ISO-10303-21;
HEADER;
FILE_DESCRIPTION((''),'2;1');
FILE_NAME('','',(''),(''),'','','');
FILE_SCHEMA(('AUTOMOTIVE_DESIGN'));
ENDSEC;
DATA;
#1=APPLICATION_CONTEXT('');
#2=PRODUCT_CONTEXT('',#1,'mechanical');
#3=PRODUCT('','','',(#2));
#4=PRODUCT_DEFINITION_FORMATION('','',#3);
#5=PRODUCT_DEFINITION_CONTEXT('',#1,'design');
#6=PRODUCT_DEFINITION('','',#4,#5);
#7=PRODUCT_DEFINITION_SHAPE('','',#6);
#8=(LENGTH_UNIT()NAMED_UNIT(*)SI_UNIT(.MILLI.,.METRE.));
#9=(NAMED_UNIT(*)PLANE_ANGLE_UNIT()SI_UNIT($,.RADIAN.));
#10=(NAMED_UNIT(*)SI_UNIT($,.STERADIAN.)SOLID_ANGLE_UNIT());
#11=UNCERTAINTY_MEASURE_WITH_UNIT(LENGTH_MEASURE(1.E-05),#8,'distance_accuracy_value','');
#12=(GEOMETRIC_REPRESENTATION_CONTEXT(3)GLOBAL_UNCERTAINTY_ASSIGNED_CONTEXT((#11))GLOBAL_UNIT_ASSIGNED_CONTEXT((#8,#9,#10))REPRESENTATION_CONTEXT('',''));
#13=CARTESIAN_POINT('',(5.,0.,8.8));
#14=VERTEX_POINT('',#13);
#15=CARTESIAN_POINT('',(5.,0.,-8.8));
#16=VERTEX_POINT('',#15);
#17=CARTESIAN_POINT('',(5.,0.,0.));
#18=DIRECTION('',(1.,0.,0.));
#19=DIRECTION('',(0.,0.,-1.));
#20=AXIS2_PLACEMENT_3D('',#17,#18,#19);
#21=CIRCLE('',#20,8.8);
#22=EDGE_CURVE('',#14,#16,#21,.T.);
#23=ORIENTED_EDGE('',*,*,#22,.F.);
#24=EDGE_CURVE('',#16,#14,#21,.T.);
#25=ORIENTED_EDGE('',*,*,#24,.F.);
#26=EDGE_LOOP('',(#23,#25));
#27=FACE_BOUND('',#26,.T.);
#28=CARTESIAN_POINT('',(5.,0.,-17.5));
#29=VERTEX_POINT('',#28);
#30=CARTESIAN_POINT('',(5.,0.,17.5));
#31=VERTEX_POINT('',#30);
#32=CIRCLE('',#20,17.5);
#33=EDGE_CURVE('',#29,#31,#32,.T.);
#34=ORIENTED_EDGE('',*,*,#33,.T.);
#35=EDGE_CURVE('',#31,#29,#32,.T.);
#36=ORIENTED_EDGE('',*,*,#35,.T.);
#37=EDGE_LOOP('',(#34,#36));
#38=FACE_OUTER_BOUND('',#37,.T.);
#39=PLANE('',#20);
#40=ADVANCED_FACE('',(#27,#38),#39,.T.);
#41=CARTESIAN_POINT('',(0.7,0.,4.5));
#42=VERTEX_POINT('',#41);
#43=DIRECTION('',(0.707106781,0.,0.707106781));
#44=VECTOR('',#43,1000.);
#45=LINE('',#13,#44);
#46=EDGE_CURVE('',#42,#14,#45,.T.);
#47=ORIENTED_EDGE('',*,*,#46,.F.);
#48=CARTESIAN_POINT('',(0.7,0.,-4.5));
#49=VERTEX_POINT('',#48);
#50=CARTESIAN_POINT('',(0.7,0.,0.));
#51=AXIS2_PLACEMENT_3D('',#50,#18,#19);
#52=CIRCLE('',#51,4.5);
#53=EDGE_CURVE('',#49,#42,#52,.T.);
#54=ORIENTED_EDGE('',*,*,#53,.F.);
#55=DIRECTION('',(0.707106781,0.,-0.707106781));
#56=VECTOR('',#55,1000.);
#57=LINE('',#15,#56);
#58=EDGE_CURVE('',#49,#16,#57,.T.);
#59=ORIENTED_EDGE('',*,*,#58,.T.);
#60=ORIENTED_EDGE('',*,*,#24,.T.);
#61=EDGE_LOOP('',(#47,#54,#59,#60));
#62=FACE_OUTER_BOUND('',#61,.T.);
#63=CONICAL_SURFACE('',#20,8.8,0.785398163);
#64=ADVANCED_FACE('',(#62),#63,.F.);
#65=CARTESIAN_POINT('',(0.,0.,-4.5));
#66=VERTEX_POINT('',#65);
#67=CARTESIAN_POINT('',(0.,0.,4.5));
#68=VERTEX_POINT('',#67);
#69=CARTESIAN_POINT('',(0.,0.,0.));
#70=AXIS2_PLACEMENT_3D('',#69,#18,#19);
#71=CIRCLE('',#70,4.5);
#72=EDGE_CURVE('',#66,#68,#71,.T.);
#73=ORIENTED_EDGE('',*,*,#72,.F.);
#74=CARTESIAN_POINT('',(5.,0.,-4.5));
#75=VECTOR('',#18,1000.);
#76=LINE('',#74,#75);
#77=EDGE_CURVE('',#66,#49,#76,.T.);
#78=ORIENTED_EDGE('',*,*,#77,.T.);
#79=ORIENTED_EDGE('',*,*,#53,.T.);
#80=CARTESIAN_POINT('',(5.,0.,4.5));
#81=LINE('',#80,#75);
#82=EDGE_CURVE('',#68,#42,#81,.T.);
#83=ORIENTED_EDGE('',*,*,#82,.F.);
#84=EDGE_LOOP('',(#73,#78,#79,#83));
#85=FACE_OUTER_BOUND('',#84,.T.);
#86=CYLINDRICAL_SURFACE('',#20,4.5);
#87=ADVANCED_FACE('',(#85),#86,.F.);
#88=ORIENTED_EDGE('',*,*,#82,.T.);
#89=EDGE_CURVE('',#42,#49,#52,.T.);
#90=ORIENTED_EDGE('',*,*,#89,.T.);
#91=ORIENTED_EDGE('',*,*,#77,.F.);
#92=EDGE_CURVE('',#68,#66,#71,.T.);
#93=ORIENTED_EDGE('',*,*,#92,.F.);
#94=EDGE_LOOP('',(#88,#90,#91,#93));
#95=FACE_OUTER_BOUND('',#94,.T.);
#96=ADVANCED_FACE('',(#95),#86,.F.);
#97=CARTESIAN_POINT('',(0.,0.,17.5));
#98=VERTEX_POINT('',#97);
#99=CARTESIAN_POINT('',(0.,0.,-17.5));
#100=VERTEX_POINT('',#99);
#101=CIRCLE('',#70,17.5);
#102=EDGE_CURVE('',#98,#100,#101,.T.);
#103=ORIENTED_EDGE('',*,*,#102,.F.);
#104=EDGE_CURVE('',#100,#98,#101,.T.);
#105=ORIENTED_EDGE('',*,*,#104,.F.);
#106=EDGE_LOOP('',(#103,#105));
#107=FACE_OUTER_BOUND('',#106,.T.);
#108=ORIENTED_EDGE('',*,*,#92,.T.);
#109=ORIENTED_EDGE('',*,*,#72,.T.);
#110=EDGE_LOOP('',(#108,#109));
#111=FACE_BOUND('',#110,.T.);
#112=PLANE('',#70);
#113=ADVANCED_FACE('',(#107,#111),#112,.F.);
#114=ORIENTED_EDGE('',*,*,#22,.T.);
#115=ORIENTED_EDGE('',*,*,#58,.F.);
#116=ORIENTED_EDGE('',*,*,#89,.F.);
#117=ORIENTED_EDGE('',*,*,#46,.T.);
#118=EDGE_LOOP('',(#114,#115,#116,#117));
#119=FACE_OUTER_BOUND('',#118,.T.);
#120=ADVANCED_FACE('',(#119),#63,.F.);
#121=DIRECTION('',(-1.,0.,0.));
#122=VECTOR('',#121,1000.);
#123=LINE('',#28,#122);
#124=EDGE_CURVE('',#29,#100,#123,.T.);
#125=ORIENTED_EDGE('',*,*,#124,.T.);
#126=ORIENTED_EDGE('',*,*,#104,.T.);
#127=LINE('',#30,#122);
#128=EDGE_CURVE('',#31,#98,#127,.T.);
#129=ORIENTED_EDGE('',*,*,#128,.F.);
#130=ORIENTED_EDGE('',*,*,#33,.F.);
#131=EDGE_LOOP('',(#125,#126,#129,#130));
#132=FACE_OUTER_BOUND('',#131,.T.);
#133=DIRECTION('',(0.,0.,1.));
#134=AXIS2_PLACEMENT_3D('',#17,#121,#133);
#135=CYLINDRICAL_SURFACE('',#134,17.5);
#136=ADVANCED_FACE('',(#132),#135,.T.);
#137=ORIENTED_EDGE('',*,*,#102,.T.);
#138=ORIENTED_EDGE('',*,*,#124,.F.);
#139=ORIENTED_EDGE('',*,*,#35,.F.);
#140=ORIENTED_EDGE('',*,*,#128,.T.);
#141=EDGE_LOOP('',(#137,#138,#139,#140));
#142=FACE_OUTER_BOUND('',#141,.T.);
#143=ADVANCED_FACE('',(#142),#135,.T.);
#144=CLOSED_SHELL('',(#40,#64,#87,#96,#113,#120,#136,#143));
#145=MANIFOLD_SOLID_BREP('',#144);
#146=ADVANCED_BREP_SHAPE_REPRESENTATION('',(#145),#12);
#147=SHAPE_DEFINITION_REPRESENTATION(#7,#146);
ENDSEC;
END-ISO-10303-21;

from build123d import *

# Parameters (mm, degrees)
SKETCH_1_R      = 17.5
EXTRUDE_1_DEPTH = 5


with BuildPart() as part:
    # 草图1 → 凸台-拉伸1 (new body)
    with BuildSketch(Plane(origin=(0, 0, 0), x_dir=(0, 0, -1), z_dir=(1, 0, 0))):
        Circle(SKETCH_1_R)
    extrude(amount=EXTRUDE_1_DEPTH)

    # 草图3 → 打孔尺寸(%根据)内六角花形沉头螺钉的类型1 (revolve, cut)
    with BuildSketch(Plane(origin=(5, 0, 0), x_dir=(0, 0, -1), z_dir=(0, 1, 0))):
        Polygon((0, 0), (0, 5), (4.5, 5), (4.5, 4.3), (8.8, 0), align=None)
    revolve(axis=Axis((11.35, 0, 0), (-1, 0, 0)), mode=Mode.SUBTRACT)


solid = part.part
